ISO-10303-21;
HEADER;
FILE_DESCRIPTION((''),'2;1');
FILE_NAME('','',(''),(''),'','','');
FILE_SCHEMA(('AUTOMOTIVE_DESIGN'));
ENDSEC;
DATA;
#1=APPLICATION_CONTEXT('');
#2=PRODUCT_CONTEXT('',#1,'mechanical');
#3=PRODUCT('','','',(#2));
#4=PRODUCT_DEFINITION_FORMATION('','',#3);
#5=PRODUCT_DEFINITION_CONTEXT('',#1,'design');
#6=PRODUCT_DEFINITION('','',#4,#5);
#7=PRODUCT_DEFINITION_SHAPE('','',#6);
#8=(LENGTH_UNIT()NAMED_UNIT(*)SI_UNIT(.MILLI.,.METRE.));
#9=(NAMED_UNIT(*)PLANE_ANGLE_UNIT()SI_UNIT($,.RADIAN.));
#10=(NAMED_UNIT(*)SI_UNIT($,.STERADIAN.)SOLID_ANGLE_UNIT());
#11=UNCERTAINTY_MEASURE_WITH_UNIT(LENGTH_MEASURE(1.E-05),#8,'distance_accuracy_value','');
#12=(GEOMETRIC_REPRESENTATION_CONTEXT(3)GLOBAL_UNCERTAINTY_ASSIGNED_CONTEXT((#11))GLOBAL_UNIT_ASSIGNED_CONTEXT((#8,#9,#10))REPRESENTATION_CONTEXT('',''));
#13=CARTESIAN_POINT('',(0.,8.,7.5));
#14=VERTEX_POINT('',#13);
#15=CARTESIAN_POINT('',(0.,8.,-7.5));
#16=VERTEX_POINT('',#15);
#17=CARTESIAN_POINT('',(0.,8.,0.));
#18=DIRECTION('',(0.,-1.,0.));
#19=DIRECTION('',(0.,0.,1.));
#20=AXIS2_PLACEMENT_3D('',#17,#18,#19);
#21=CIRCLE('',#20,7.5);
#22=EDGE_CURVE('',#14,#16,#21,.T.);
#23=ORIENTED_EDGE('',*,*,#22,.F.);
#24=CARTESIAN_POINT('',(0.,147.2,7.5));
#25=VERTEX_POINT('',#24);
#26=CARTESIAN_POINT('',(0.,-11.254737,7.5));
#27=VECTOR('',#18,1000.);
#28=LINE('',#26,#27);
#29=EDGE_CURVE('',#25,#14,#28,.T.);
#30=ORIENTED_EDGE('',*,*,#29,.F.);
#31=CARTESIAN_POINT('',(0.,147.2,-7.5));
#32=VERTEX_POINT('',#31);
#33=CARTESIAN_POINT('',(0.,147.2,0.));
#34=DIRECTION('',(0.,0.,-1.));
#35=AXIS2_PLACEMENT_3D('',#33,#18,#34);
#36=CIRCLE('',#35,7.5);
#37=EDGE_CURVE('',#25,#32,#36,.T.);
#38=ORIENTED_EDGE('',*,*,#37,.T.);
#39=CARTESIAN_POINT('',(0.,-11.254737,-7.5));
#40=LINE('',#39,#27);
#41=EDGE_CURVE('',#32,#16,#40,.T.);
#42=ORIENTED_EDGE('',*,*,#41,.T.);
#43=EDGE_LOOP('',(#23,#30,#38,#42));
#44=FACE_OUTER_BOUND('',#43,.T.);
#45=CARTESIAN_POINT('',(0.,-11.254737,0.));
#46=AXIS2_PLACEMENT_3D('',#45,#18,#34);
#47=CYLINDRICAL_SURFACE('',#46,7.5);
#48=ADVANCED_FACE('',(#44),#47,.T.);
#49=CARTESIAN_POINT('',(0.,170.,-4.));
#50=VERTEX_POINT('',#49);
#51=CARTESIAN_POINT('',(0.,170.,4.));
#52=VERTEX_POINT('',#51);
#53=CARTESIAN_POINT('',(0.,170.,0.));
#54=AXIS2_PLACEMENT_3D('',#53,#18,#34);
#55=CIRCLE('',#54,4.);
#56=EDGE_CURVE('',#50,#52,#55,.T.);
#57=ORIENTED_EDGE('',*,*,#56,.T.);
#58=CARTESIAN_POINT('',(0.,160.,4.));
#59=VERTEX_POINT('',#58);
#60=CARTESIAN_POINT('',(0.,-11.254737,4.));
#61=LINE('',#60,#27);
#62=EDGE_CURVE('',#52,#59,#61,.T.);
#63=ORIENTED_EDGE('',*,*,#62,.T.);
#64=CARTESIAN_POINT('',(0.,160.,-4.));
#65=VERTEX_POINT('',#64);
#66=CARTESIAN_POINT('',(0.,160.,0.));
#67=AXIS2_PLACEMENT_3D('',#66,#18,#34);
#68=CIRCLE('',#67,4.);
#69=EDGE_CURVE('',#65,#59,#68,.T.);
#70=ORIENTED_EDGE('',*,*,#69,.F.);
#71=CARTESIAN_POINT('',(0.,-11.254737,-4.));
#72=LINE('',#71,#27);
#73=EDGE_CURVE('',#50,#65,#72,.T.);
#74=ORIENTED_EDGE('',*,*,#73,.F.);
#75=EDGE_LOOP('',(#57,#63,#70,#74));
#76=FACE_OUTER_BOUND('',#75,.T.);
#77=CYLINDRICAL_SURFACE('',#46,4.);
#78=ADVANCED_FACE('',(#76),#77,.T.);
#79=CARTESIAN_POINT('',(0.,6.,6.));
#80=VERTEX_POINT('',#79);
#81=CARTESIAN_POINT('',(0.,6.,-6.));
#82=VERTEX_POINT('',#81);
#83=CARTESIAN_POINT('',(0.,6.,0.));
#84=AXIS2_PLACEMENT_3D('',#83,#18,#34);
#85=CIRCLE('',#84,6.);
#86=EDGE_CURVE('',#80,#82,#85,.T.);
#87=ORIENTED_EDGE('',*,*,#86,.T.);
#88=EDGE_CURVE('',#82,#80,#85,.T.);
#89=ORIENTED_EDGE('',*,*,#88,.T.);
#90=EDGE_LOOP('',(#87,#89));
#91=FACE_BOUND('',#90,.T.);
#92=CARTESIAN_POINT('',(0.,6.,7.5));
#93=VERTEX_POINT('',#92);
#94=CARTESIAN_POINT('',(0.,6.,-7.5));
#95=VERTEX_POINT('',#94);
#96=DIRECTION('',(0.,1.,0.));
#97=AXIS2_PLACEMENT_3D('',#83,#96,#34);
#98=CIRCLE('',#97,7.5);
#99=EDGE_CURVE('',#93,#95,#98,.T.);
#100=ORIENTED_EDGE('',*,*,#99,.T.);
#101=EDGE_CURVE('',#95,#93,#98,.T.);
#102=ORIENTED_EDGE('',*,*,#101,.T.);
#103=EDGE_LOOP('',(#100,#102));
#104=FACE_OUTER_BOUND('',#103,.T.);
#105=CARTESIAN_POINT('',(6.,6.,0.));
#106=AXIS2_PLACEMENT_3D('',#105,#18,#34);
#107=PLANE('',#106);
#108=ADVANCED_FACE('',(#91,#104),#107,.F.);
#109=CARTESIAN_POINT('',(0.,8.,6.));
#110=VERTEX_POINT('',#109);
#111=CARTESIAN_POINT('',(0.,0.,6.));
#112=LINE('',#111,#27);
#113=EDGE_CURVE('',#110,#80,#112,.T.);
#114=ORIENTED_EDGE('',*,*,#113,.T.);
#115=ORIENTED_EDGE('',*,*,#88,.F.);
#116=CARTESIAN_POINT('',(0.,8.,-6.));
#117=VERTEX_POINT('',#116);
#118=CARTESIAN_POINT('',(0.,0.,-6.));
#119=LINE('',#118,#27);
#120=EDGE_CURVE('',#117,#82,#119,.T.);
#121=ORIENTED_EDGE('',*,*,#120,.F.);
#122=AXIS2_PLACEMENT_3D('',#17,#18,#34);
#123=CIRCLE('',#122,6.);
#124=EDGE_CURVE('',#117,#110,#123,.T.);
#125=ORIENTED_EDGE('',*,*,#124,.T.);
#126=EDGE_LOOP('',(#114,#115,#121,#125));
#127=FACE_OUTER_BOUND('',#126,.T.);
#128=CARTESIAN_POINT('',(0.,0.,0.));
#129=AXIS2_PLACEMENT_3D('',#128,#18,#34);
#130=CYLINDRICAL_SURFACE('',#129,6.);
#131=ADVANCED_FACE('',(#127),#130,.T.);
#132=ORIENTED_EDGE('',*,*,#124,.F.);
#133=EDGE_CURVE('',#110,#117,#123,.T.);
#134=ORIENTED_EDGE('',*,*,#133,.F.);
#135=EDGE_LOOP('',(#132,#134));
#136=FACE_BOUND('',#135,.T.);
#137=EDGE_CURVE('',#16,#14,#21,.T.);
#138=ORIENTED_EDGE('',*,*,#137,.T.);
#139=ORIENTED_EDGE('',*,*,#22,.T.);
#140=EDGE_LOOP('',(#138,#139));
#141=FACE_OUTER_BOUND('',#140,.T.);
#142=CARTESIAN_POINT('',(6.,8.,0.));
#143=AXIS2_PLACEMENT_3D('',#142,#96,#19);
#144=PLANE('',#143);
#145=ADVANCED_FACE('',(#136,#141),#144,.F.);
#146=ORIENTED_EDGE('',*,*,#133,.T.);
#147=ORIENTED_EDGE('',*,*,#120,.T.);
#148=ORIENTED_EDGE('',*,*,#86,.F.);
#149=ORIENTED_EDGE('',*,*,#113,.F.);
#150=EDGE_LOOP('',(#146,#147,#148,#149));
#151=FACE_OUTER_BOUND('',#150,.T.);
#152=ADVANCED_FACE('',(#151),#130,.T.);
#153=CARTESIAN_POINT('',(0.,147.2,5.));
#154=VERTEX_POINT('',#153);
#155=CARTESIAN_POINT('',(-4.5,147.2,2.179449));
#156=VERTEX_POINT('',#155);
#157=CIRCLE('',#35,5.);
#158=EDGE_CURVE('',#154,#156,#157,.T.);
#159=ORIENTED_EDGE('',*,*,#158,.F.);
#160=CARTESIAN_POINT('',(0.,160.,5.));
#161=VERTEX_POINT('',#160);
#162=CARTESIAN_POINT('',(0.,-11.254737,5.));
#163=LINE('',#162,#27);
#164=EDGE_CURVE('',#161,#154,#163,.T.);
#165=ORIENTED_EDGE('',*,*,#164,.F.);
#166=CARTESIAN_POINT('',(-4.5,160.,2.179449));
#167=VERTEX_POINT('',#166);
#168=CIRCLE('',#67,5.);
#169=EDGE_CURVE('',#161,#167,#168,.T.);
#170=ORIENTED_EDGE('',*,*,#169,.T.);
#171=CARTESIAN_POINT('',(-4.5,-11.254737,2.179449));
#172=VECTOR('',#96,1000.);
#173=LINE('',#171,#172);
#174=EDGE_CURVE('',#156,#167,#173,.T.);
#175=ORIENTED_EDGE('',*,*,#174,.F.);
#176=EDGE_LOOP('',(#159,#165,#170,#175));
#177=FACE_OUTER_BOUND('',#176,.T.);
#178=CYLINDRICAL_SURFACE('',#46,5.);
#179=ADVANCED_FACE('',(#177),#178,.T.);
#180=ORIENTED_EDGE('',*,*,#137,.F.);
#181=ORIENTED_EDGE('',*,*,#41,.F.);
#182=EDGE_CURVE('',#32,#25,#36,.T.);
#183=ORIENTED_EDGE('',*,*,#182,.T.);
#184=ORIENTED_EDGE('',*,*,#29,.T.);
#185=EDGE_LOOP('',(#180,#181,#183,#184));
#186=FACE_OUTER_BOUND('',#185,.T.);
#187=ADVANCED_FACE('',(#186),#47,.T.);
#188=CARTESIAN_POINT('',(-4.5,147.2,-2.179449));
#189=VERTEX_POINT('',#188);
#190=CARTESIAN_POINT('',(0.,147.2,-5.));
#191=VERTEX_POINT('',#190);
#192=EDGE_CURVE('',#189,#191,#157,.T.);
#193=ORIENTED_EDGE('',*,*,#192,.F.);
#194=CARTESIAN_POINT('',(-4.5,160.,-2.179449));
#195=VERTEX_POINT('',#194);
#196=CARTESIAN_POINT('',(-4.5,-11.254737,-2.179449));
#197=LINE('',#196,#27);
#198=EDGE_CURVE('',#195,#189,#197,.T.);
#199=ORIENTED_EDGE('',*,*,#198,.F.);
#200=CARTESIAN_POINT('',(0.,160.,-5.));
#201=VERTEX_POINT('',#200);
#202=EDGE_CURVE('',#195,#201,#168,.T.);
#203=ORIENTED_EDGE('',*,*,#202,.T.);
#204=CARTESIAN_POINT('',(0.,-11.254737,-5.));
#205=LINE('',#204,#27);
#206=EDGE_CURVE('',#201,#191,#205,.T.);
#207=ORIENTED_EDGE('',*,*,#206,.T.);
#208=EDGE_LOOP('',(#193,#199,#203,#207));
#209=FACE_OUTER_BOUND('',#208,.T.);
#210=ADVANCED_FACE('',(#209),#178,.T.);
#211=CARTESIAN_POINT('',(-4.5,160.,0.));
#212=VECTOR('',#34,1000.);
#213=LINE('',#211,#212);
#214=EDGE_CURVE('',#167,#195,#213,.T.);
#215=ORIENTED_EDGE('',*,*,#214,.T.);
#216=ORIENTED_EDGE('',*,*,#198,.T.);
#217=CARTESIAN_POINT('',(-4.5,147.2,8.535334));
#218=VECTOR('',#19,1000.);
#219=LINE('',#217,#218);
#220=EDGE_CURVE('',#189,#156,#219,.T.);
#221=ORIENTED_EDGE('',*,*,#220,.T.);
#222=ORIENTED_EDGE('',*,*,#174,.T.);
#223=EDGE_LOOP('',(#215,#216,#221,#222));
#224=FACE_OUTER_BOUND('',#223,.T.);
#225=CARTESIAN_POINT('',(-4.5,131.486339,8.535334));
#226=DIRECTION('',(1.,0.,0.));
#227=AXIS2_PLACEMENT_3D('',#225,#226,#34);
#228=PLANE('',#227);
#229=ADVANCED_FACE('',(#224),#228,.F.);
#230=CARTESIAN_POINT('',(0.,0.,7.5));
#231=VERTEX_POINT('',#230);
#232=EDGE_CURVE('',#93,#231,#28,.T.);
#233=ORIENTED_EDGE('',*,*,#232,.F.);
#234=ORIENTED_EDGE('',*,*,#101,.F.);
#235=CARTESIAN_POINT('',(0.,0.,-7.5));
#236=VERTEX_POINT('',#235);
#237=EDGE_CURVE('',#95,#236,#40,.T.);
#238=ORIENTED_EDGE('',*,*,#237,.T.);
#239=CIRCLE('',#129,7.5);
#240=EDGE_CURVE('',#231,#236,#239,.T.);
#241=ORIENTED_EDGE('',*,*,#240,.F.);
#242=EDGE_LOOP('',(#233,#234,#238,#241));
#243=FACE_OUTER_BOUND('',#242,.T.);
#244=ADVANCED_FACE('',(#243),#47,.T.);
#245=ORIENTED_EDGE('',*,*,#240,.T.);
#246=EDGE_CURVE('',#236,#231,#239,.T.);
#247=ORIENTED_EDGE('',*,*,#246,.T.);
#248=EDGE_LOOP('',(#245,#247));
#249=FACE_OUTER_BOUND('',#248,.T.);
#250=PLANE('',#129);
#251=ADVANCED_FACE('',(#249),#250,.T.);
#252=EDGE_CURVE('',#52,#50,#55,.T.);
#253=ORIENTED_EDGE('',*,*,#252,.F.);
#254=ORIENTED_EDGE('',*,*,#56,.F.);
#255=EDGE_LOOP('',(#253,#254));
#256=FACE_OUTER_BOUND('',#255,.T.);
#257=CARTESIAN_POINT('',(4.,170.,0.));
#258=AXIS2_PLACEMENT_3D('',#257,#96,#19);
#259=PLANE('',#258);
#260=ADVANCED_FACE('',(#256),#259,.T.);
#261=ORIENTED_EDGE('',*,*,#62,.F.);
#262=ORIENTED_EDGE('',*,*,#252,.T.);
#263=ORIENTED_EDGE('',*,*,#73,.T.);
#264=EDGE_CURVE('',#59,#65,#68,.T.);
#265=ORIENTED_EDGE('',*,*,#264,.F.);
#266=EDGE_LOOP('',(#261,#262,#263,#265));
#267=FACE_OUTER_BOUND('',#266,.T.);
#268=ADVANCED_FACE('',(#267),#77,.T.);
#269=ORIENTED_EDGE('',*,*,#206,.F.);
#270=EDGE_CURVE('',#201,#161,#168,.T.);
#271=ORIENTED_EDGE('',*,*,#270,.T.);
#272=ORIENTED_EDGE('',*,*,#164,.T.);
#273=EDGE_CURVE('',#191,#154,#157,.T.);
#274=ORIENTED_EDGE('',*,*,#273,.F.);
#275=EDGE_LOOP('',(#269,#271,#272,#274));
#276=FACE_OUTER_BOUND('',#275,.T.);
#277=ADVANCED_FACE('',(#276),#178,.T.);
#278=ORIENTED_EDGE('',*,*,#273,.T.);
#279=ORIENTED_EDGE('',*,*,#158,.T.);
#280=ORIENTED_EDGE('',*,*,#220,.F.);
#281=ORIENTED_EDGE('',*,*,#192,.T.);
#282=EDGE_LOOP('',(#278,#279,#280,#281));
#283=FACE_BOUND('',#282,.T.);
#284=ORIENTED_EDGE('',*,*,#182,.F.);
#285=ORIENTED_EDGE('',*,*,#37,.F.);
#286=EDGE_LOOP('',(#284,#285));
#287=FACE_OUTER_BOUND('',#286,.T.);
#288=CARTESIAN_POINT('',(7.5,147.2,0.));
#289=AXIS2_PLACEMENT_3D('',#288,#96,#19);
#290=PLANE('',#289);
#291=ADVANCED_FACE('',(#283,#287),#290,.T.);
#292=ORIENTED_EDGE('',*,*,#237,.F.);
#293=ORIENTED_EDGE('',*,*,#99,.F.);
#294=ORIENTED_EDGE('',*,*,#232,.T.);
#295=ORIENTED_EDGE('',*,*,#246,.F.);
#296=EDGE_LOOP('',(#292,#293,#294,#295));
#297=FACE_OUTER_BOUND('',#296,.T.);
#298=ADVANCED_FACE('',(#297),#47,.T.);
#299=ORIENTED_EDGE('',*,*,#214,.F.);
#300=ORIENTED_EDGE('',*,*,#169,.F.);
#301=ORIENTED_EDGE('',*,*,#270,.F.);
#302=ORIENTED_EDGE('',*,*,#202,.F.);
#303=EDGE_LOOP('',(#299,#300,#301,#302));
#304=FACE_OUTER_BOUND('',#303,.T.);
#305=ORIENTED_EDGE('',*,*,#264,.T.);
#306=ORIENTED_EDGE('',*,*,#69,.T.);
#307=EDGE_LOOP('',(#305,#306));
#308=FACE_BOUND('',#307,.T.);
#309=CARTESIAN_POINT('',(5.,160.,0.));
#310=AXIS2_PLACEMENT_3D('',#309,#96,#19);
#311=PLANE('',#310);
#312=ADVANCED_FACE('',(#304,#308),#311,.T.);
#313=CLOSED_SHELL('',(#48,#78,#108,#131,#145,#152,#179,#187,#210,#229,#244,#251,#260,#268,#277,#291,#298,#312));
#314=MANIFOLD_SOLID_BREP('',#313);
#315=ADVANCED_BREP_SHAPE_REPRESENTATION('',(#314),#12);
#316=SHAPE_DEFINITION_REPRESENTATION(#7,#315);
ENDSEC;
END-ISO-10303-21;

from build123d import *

# Parameters (mm, degrees)
SKETCH2_W          = 3.587001172
SKETCH2_H          = 15.298776085
CUT_EXTRUDE1_DEPTH = 12.8
SKETCH3_W          = 4.275598186
SKETCH3_H          = 2


with BuildPart() as part:
    # Sketch1 → Revolve1 (revolve)
    with BuildSketch(Plane.XY, mode=Mode.PRIVATE) as revolve1_sk:
        Polygon((0, 0), (7.5, 0), (7.5, 147.2), (5, 147.2), (5, 160), (4, 160), (4, 170), (0, 170), align=None)
    revolve(revolve1_sk.sketch.rotate(Axis((0, -11.254736842, 0), (0, 1, 0)), 90), axis=Axis((0, -11.254736842, 0), (0, 1, 0)))

    # Sketch2 → Cut-Extrude1 (cut)
    with BuildSketch(Plane(origin=(0, 160, 0), x_dir=(1, 0, 0), z_dir=(0, 1, 0))):
        with Locations((-6.293500586, -0.885946073)):
            Rectangle(SKETCH2_W, SKETCH2_H)
    extrude(amount=-CUT_EXTRUDE1_DEPTH, mode=Mode.SUBTRACT)

    # Sketch3 → Cut-Revolve1 (revolve, cut)
    with BuildSketch(Plane.XY, mode=Mode.PRIVATE) as cut_revolve1_sk:
        with Locations((8.137799093, 7)):
            Rectangle(SKETCH3_W, SKETCH3_H)
    revolve(cut_revolve1_sk.sketch.rotate(Axis((0, 0, 0), (0, 1, 0)), 90), axis=Axis((0, 0, 0), (0, 1, 0)), mode=Mode.SUBTRACT)


solid = part.part
